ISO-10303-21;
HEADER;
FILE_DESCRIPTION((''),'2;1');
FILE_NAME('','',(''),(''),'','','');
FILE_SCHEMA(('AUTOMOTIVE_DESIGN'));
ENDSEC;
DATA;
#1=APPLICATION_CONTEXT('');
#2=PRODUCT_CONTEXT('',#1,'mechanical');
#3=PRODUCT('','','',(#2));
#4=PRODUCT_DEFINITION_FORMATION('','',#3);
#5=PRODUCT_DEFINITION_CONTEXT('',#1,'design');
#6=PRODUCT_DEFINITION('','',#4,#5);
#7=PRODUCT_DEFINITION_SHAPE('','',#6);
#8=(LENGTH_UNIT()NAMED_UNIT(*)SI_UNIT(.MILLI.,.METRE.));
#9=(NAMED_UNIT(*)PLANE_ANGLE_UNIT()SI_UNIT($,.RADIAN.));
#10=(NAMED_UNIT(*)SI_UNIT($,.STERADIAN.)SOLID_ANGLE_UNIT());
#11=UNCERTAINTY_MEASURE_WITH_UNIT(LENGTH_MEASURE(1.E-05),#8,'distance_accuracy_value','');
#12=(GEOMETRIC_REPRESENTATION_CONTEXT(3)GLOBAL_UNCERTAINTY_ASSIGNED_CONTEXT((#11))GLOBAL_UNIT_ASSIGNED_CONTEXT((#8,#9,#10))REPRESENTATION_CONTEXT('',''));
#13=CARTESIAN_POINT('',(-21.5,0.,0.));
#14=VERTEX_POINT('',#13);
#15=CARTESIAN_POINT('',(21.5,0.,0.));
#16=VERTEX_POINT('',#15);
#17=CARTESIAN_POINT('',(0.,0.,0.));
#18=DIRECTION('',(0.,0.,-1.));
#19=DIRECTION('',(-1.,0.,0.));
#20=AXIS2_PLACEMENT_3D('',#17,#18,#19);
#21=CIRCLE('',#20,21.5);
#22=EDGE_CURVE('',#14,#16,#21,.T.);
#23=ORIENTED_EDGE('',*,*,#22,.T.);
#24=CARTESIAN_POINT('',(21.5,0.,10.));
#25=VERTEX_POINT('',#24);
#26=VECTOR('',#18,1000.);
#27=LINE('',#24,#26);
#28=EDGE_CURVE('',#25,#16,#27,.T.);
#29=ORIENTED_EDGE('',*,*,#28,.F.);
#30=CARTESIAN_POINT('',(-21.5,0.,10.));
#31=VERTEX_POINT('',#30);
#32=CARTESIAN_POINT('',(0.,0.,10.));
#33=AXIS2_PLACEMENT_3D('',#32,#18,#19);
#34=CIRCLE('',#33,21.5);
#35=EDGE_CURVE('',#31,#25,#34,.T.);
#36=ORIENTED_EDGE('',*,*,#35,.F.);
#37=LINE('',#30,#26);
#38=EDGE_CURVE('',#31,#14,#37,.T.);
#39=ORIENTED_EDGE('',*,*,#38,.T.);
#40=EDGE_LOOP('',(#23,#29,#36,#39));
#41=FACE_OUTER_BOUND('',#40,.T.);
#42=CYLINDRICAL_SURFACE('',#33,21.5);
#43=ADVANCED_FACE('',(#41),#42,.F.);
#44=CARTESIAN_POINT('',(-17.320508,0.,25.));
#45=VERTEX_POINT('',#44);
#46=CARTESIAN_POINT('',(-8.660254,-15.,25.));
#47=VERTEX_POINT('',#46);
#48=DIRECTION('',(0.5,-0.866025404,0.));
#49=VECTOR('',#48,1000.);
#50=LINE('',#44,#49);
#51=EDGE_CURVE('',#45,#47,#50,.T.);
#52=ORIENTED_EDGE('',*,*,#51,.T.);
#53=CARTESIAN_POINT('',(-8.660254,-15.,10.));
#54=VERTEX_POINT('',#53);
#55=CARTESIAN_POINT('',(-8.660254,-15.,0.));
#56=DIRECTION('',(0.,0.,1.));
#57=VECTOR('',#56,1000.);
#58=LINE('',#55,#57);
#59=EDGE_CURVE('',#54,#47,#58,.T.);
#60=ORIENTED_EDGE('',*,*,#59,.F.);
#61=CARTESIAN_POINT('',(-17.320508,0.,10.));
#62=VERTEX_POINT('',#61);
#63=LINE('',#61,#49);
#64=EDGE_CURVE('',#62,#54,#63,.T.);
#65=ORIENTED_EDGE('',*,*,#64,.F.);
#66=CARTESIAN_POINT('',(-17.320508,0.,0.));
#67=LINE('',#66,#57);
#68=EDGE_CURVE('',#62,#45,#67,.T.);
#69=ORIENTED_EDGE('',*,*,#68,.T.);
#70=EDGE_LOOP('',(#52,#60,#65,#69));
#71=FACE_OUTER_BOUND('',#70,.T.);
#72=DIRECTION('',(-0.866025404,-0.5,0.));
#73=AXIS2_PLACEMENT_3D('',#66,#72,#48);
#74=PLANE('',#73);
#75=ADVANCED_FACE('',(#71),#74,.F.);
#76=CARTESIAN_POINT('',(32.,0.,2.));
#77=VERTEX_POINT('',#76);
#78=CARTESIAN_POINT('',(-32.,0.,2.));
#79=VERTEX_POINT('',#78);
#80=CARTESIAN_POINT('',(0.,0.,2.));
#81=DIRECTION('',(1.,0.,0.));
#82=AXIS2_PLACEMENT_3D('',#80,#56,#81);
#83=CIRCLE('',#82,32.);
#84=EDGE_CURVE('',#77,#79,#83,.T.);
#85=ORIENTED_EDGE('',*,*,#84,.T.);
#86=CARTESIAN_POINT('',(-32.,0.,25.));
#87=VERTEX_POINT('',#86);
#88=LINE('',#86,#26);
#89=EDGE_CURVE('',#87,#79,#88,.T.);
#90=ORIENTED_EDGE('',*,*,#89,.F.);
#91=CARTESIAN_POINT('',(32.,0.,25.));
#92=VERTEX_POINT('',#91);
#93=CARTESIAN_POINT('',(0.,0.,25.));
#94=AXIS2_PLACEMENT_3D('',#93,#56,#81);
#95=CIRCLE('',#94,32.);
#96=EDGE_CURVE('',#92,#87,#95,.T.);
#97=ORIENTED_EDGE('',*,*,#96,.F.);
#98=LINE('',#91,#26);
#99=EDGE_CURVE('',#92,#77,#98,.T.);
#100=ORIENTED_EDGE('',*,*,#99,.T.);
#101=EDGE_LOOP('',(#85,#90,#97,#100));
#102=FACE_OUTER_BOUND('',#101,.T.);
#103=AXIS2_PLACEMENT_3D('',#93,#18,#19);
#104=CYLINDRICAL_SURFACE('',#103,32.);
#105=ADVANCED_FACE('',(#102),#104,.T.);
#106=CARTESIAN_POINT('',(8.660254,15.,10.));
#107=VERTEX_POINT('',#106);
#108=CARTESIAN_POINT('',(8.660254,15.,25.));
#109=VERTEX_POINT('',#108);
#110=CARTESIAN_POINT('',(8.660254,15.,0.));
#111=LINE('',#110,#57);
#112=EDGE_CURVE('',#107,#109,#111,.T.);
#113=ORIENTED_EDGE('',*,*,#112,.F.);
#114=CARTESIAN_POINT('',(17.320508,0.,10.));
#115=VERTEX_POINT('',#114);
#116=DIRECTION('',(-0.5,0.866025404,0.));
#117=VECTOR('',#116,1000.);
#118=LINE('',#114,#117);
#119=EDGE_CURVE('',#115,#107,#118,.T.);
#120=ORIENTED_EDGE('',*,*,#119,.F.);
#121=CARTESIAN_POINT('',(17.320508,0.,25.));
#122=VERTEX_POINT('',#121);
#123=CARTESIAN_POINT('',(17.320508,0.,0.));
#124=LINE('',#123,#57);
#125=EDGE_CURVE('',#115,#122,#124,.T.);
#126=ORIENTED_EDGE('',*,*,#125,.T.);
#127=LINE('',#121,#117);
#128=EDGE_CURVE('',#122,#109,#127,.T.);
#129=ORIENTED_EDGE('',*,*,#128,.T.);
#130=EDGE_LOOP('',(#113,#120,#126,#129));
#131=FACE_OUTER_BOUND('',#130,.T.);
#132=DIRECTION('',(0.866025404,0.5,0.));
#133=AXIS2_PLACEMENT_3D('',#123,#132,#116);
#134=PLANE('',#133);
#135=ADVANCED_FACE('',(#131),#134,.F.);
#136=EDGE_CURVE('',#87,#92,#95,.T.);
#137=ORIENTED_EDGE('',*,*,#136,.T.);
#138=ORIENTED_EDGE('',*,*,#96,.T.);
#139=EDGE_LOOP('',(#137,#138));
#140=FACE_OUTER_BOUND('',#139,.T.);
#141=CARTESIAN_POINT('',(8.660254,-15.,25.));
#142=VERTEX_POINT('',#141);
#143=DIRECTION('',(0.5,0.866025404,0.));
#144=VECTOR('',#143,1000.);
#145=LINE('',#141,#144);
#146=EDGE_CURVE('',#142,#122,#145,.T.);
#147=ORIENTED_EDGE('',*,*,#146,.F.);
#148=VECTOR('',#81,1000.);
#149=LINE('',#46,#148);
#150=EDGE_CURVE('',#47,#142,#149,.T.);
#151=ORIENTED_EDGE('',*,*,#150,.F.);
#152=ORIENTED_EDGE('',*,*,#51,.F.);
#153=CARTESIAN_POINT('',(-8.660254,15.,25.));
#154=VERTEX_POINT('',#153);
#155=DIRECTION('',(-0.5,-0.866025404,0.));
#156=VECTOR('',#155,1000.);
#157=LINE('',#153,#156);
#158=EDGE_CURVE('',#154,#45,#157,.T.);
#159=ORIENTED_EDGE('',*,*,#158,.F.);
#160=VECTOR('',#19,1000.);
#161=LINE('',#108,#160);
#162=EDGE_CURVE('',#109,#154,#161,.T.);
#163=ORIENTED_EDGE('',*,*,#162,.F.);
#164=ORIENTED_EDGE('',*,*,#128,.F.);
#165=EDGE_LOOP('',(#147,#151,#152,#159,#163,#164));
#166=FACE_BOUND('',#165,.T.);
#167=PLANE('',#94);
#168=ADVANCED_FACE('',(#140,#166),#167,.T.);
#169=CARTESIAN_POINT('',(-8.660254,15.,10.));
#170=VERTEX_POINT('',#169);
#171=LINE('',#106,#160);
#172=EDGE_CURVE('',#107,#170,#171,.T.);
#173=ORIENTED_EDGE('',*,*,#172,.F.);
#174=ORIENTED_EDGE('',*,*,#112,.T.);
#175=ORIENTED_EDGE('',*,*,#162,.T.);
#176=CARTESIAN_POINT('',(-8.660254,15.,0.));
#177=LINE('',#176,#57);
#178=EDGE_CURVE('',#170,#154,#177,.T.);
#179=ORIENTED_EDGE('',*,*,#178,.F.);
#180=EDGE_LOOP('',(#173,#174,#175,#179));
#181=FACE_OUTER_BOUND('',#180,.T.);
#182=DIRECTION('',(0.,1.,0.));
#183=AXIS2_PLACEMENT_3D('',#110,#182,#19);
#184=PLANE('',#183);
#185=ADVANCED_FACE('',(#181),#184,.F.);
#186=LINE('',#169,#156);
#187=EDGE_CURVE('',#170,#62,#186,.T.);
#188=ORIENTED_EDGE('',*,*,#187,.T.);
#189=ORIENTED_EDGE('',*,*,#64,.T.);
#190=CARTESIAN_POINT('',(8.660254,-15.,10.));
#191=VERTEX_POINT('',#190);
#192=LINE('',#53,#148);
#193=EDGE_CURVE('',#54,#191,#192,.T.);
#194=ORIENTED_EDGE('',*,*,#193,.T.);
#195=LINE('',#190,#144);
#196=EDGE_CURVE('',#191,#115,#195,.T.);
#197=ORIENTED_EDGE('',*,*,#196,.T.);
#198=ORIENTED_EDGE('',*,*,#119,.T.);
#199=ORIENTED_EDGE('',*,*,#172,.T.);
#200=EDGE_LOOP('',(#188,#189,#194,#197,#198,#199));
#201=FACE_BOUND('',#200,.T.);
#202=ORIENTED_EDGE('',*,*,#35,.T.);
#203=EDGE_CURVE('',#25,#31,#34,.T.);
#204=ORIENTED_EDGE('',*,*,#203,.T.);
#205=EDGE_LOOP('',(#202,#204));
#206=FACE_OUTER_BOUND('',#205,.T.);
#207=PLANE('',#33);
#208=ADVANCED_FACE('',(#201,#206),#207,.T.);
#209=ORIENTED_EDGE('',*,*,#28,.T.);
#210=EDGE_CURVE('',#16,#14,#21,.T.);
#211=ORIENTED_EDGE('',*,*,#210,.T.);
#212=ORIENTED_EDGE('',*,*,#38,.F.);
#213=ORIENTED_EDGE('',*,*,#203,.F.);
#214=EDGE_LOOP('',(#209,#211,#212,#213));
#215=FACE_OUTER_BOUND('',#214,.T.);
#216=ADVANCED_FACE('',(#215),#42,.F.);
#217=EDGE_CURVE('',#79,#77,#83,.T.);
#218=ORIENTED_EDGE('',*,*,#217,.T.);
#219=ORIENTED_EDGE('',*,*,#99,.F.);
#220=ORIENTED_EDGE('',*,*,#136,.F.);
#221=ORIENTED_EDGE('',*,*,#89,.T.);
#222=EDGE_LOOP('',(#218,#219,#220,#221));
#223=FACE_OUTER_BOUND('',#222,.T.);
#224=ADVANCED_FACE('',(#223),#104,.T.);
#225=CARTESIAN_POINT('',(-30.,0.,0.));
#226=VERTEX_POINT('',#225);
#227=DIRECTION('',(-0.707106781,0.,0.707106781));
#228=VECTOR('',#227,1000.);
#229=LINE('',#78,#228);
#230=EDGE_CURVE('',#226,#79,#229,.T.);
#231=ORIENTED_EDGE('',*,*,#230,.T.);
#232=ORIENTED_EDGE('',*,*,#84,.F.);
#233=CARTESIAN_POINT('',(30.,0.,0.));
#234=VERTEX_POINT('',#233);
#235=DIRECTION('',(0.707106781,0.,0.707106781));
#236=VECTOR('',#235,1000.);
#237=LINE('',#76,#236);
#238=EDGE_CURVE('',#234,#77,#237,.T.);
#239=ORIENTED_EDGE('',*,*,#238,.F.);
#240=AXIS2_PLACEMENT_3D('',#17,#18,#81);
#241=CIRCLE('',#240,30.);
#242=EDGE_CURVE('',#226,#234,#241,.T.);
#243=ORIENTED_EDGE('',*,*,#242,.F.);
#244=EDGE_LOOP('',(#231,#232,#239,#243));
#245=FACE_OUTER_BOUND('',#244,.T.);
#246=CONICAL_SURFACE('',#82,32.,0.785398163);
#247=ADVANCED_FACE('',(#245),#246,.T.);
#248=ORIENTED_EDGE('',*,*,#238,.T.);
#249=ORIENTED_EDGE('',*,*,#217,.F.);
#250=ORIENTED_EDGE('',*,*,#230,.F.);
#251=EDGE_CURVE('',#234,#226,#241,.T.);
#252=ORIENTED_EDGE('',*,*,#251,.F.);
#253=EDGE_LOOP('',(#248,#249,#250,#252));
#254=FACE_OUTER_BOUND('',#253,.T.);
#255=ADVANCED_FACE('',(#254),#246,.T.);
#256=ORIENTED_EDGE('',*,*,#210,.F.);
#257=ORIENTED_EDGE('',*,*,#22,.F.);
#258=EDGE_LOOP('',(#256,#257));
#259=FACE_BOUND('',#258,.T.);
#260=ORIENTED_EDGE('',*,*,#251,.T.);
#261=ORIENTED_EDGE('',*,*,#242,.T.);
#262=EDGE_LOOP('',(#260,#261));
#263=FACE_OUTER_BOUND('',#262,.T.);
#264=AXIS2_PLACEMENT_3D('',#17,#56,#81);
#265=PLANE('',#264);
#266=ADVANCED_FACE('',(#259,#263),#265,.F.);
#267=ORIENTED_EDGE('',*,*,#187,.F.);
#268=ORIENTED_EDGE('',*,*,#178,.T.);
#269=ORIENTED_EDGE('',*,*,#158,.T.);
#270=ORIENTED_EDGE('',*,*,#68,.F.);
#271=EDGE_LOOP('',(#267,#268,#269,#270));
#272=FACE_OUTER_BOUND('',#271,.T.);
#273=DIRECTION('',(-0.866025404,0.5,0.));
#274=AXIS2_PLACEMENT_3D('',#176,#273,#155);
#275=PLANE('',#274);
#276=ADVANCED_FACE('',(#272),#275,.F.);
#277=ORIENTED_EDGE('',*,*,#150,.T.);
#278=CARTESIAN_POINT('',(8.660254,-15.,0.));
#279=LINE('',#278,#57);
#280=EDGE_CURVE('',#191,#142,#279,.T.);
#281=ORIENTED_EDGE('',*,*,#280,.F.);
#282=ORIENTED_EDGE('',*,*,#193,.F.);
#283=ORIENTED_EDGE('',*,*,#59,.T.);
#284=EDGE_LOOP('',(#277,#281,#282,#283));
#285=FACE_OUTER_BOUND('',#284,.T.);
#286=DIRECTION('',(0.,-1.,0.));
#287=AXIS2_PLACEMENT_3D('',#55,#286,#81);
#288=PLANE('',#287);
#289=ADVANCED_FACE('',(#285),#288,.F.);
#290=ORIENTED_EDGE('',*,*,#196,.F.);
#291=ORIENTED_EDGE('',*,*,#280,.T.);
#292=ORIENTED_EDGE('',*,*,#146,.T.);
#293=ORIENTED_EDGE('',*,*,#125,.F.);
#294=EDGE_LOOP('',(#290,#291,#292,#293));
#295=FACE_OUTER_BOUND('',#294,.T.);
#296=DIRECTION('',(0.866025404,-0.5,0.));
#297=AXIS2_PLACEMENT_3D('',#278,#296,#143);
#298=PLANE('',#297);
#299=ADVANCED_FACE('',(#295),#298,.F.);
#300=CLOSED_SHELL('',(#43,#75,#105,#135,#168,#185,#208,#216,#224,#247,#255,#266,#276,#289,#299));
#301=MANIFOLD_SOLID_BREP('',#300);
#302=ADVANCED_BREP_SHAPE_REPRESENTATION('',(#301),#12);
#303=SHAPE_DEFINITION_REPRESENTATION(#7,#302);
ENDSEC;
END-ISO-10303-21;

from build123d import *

# Parameters (mm, degrees)
SKETCH_1_R          = 32
EXTRUDE_1_DEPTH     = 25
CUT_EXTRUDE_1_DEPTH = 52.701063819
SKETCH_3_R          = 21.5
CUT_EXTRUDE_2_DEPTH = 10
CHAMFER_1_SIZE      = 2


with BuildPart() as part:
    # 草图1 → 凸台-拉伸1 (new body)
    with BuildSketch(Plane.XY):
        Circle(SKETCH_1_R)
    extrude(amount=EXTRUDE_1_DEPTH)

    # 草图2 → 切除-拉伸1 (cut, through all)
    with BuildSketch(Plane.XY.offset(25)):
        Polygon((17.320508076, 0), (8.660254038, 15), (-8.660254038, 15), (-17.320508076, 0), (-8.660254038, -15), (8.660254038, -15), align=None)
    extrude(amount=-CUT_EXTRUDE_1_DEPTH, mode=Mode.SUBTRACT)

    # 草图3 → 切除-拉伸2 (cut)
    with BuildSketch(Plane(origin=(0, 0, 0), x_dir=(-1, 0, 0), z_dir=(0, 0, -1))):
        Circle(SKETCH_3_R)
    extrude(amount=-CUT_EXTRUDE_2_DEPTH, mode=Mode.SUBTRACT)

    # 倒角1
    chamfer_1_edges = [part.edges().sort_by_distance(p)[0] for p in [
        (-32, 0, 0),
    ]]
    chamfer(chamfer_1_edges, length=CHAMFER_1_SIZE)


solid = part.part
